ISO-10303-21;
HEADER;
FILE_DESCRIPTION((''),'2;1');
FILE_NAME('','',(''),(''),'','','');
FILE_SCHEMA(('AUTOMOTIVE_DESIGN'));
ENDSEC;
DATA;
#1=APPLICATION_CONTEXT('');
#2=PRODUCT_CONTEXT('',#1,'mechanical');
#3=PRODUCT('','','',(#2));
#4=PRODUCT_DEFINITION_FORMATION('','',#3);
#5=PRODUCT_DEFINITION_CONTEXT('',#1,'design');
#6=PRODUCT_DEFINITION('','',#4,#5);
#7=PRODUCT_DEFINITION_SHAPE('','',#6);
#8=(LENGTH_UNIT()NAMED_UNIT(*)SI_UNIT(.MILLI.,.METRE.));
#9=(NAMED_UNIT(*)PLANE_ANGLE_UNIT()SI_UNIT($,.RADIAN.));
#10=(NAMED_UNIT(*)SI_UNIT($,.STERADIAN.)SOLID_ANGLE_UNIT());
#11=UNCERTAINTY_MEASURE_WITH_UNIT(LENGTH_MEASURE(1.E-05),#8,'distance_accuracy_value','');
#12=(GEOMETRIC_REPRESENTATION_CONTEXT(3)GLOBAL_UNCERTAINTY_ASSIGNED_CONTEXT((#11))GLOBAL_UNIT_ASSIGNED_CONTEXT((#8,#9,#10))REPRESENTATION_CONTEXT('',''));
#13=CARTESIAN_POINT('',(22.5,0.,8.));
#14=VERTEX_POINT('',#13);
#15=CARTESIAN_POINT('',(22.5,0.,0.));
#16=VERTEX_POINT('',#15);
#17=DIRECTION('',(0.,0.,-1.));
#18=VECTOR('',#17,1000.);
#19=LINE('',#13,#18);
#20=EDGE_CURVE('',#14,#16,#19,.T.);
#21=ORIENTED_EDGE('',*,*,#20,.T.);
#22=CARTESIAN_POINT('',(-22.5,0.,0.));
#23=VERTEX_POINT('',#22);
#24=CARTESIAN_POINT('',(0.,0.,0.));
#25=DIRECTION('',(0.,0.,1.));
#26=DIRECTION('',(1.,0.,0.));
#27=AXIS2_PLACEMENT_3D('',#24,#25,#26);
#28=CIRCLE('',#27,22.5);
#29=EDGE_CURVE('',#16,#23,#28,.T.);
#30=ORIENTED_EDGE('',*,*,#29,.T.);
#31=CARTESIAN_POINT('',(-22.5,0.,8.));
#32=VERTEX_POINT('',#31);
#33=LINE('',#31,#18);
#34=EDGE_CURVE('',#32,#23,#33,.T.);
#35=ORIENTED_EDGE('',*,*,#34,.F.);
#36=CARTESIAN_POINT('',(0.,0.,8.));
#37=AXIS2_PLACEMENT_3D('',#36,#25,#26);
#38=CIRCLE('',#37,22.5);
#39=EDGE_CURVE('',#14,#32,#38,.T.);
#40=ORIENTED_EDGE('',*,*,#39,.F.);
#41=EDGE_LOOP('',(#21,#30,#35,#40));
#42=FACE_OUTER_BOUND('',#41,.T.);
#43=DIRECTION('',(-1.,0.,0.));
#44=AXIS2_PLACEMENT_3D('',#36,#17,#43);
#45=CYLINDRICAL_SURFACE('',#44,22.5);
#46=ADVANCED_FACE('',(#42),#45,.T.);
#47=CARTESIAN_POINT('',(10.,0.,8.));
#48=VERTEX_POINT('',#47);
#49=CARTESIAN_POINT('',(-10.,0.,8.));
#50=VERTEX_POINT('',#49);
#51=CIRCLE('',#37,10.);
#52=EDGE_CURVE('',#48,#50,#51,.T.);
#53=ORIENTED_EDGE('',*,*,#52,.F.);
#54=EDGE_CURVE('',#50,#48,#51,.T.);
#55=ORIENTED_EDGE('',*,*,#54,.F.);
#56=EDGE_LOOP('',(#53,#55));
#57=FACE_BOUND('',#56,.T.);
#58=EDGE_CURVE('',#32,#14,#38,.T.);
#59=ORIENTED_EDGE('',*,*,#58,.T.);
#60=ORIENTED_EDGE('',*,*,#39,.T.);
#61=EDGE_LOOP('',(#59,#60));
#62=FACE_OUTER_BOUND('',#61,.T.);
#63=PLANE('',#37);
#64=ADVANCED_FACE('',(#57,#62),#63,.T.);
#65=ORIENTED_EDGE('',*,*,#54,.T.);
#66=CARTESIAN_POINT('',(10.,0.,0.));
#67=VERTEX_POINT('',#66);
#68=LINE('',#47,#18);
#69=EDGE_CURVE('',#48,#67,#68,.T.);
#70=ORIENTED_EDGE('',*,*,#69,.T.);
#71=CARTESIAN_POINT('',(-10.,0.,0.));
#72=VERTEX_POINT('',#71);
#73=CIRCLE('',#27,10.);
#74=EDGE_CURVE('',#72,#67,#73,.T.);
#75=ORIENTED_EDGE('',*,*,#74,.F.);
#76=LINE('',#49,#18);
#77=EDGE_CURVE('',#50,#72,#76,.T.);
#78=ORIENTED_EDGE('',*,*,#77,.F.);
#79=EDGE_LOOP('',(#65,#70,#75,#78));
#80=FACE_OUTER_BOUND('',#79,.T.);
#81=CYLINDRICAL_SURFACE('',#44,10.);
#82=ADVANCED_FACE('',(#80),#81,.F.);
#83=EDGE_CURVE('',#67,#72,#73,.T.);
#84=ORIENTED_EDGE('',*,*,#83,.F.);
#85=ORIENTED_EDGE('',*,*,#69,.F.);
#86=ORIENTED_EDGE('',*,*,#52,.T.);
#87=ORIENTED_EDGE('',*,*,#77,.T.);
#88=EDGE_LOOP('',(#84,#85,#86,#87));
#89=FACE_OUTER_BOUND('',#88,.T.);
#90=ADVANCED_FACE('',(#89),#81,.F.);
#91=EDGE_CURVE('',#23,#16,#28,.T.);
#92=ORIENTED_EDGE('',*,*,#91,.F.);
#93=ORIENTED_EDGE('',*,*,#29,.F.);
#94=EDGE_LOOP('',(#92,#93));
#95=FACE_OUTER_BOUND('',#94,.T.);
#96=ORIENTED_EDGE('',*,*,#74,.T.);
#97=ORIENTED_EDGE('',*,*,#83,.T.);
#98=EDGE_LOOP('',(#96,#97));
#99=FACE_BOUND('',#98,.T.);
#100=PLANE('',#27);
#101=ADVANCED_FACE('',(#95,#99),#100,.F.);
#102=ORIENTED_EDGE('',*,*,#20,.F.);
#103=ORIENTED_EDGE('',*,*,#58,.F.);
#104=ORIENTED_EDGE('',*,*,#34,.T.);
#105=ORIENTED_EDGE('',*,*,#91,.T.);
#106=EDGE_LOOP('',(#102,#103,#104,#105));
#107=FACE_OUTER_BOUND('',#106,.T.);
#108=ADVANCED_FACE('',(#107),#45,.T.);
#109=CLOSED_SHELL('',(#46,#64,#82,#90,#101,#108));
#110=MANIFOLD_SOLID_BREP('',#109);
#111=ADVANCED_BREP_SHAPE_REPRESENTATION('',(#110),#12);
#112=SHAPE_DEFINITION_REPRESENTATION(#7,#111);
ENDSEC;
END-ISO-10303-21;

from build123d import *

# Parameters (mm, degrees)
WASHER_PROFILE_45_20_R   = 22.5
WASHER_PROFILE_45_20_R_2 = 10
WASHER_BODY_8MM_DEPTH    = 8


with BuildPart() as part:
    # Washer Profile Ø45-Ø20 → Washer Body 8mm (new body)
    with BuildSketch(Plane.XY):
        Circle(WASHER_PROFILE_45_20_R)
        Circle(WASHER_PROFILE_45_20_R_2, mode=Mode.SUBTRACT)
    extrude(amount=WASHER_BODY_8MM_DEPTH)


solid = part.part
